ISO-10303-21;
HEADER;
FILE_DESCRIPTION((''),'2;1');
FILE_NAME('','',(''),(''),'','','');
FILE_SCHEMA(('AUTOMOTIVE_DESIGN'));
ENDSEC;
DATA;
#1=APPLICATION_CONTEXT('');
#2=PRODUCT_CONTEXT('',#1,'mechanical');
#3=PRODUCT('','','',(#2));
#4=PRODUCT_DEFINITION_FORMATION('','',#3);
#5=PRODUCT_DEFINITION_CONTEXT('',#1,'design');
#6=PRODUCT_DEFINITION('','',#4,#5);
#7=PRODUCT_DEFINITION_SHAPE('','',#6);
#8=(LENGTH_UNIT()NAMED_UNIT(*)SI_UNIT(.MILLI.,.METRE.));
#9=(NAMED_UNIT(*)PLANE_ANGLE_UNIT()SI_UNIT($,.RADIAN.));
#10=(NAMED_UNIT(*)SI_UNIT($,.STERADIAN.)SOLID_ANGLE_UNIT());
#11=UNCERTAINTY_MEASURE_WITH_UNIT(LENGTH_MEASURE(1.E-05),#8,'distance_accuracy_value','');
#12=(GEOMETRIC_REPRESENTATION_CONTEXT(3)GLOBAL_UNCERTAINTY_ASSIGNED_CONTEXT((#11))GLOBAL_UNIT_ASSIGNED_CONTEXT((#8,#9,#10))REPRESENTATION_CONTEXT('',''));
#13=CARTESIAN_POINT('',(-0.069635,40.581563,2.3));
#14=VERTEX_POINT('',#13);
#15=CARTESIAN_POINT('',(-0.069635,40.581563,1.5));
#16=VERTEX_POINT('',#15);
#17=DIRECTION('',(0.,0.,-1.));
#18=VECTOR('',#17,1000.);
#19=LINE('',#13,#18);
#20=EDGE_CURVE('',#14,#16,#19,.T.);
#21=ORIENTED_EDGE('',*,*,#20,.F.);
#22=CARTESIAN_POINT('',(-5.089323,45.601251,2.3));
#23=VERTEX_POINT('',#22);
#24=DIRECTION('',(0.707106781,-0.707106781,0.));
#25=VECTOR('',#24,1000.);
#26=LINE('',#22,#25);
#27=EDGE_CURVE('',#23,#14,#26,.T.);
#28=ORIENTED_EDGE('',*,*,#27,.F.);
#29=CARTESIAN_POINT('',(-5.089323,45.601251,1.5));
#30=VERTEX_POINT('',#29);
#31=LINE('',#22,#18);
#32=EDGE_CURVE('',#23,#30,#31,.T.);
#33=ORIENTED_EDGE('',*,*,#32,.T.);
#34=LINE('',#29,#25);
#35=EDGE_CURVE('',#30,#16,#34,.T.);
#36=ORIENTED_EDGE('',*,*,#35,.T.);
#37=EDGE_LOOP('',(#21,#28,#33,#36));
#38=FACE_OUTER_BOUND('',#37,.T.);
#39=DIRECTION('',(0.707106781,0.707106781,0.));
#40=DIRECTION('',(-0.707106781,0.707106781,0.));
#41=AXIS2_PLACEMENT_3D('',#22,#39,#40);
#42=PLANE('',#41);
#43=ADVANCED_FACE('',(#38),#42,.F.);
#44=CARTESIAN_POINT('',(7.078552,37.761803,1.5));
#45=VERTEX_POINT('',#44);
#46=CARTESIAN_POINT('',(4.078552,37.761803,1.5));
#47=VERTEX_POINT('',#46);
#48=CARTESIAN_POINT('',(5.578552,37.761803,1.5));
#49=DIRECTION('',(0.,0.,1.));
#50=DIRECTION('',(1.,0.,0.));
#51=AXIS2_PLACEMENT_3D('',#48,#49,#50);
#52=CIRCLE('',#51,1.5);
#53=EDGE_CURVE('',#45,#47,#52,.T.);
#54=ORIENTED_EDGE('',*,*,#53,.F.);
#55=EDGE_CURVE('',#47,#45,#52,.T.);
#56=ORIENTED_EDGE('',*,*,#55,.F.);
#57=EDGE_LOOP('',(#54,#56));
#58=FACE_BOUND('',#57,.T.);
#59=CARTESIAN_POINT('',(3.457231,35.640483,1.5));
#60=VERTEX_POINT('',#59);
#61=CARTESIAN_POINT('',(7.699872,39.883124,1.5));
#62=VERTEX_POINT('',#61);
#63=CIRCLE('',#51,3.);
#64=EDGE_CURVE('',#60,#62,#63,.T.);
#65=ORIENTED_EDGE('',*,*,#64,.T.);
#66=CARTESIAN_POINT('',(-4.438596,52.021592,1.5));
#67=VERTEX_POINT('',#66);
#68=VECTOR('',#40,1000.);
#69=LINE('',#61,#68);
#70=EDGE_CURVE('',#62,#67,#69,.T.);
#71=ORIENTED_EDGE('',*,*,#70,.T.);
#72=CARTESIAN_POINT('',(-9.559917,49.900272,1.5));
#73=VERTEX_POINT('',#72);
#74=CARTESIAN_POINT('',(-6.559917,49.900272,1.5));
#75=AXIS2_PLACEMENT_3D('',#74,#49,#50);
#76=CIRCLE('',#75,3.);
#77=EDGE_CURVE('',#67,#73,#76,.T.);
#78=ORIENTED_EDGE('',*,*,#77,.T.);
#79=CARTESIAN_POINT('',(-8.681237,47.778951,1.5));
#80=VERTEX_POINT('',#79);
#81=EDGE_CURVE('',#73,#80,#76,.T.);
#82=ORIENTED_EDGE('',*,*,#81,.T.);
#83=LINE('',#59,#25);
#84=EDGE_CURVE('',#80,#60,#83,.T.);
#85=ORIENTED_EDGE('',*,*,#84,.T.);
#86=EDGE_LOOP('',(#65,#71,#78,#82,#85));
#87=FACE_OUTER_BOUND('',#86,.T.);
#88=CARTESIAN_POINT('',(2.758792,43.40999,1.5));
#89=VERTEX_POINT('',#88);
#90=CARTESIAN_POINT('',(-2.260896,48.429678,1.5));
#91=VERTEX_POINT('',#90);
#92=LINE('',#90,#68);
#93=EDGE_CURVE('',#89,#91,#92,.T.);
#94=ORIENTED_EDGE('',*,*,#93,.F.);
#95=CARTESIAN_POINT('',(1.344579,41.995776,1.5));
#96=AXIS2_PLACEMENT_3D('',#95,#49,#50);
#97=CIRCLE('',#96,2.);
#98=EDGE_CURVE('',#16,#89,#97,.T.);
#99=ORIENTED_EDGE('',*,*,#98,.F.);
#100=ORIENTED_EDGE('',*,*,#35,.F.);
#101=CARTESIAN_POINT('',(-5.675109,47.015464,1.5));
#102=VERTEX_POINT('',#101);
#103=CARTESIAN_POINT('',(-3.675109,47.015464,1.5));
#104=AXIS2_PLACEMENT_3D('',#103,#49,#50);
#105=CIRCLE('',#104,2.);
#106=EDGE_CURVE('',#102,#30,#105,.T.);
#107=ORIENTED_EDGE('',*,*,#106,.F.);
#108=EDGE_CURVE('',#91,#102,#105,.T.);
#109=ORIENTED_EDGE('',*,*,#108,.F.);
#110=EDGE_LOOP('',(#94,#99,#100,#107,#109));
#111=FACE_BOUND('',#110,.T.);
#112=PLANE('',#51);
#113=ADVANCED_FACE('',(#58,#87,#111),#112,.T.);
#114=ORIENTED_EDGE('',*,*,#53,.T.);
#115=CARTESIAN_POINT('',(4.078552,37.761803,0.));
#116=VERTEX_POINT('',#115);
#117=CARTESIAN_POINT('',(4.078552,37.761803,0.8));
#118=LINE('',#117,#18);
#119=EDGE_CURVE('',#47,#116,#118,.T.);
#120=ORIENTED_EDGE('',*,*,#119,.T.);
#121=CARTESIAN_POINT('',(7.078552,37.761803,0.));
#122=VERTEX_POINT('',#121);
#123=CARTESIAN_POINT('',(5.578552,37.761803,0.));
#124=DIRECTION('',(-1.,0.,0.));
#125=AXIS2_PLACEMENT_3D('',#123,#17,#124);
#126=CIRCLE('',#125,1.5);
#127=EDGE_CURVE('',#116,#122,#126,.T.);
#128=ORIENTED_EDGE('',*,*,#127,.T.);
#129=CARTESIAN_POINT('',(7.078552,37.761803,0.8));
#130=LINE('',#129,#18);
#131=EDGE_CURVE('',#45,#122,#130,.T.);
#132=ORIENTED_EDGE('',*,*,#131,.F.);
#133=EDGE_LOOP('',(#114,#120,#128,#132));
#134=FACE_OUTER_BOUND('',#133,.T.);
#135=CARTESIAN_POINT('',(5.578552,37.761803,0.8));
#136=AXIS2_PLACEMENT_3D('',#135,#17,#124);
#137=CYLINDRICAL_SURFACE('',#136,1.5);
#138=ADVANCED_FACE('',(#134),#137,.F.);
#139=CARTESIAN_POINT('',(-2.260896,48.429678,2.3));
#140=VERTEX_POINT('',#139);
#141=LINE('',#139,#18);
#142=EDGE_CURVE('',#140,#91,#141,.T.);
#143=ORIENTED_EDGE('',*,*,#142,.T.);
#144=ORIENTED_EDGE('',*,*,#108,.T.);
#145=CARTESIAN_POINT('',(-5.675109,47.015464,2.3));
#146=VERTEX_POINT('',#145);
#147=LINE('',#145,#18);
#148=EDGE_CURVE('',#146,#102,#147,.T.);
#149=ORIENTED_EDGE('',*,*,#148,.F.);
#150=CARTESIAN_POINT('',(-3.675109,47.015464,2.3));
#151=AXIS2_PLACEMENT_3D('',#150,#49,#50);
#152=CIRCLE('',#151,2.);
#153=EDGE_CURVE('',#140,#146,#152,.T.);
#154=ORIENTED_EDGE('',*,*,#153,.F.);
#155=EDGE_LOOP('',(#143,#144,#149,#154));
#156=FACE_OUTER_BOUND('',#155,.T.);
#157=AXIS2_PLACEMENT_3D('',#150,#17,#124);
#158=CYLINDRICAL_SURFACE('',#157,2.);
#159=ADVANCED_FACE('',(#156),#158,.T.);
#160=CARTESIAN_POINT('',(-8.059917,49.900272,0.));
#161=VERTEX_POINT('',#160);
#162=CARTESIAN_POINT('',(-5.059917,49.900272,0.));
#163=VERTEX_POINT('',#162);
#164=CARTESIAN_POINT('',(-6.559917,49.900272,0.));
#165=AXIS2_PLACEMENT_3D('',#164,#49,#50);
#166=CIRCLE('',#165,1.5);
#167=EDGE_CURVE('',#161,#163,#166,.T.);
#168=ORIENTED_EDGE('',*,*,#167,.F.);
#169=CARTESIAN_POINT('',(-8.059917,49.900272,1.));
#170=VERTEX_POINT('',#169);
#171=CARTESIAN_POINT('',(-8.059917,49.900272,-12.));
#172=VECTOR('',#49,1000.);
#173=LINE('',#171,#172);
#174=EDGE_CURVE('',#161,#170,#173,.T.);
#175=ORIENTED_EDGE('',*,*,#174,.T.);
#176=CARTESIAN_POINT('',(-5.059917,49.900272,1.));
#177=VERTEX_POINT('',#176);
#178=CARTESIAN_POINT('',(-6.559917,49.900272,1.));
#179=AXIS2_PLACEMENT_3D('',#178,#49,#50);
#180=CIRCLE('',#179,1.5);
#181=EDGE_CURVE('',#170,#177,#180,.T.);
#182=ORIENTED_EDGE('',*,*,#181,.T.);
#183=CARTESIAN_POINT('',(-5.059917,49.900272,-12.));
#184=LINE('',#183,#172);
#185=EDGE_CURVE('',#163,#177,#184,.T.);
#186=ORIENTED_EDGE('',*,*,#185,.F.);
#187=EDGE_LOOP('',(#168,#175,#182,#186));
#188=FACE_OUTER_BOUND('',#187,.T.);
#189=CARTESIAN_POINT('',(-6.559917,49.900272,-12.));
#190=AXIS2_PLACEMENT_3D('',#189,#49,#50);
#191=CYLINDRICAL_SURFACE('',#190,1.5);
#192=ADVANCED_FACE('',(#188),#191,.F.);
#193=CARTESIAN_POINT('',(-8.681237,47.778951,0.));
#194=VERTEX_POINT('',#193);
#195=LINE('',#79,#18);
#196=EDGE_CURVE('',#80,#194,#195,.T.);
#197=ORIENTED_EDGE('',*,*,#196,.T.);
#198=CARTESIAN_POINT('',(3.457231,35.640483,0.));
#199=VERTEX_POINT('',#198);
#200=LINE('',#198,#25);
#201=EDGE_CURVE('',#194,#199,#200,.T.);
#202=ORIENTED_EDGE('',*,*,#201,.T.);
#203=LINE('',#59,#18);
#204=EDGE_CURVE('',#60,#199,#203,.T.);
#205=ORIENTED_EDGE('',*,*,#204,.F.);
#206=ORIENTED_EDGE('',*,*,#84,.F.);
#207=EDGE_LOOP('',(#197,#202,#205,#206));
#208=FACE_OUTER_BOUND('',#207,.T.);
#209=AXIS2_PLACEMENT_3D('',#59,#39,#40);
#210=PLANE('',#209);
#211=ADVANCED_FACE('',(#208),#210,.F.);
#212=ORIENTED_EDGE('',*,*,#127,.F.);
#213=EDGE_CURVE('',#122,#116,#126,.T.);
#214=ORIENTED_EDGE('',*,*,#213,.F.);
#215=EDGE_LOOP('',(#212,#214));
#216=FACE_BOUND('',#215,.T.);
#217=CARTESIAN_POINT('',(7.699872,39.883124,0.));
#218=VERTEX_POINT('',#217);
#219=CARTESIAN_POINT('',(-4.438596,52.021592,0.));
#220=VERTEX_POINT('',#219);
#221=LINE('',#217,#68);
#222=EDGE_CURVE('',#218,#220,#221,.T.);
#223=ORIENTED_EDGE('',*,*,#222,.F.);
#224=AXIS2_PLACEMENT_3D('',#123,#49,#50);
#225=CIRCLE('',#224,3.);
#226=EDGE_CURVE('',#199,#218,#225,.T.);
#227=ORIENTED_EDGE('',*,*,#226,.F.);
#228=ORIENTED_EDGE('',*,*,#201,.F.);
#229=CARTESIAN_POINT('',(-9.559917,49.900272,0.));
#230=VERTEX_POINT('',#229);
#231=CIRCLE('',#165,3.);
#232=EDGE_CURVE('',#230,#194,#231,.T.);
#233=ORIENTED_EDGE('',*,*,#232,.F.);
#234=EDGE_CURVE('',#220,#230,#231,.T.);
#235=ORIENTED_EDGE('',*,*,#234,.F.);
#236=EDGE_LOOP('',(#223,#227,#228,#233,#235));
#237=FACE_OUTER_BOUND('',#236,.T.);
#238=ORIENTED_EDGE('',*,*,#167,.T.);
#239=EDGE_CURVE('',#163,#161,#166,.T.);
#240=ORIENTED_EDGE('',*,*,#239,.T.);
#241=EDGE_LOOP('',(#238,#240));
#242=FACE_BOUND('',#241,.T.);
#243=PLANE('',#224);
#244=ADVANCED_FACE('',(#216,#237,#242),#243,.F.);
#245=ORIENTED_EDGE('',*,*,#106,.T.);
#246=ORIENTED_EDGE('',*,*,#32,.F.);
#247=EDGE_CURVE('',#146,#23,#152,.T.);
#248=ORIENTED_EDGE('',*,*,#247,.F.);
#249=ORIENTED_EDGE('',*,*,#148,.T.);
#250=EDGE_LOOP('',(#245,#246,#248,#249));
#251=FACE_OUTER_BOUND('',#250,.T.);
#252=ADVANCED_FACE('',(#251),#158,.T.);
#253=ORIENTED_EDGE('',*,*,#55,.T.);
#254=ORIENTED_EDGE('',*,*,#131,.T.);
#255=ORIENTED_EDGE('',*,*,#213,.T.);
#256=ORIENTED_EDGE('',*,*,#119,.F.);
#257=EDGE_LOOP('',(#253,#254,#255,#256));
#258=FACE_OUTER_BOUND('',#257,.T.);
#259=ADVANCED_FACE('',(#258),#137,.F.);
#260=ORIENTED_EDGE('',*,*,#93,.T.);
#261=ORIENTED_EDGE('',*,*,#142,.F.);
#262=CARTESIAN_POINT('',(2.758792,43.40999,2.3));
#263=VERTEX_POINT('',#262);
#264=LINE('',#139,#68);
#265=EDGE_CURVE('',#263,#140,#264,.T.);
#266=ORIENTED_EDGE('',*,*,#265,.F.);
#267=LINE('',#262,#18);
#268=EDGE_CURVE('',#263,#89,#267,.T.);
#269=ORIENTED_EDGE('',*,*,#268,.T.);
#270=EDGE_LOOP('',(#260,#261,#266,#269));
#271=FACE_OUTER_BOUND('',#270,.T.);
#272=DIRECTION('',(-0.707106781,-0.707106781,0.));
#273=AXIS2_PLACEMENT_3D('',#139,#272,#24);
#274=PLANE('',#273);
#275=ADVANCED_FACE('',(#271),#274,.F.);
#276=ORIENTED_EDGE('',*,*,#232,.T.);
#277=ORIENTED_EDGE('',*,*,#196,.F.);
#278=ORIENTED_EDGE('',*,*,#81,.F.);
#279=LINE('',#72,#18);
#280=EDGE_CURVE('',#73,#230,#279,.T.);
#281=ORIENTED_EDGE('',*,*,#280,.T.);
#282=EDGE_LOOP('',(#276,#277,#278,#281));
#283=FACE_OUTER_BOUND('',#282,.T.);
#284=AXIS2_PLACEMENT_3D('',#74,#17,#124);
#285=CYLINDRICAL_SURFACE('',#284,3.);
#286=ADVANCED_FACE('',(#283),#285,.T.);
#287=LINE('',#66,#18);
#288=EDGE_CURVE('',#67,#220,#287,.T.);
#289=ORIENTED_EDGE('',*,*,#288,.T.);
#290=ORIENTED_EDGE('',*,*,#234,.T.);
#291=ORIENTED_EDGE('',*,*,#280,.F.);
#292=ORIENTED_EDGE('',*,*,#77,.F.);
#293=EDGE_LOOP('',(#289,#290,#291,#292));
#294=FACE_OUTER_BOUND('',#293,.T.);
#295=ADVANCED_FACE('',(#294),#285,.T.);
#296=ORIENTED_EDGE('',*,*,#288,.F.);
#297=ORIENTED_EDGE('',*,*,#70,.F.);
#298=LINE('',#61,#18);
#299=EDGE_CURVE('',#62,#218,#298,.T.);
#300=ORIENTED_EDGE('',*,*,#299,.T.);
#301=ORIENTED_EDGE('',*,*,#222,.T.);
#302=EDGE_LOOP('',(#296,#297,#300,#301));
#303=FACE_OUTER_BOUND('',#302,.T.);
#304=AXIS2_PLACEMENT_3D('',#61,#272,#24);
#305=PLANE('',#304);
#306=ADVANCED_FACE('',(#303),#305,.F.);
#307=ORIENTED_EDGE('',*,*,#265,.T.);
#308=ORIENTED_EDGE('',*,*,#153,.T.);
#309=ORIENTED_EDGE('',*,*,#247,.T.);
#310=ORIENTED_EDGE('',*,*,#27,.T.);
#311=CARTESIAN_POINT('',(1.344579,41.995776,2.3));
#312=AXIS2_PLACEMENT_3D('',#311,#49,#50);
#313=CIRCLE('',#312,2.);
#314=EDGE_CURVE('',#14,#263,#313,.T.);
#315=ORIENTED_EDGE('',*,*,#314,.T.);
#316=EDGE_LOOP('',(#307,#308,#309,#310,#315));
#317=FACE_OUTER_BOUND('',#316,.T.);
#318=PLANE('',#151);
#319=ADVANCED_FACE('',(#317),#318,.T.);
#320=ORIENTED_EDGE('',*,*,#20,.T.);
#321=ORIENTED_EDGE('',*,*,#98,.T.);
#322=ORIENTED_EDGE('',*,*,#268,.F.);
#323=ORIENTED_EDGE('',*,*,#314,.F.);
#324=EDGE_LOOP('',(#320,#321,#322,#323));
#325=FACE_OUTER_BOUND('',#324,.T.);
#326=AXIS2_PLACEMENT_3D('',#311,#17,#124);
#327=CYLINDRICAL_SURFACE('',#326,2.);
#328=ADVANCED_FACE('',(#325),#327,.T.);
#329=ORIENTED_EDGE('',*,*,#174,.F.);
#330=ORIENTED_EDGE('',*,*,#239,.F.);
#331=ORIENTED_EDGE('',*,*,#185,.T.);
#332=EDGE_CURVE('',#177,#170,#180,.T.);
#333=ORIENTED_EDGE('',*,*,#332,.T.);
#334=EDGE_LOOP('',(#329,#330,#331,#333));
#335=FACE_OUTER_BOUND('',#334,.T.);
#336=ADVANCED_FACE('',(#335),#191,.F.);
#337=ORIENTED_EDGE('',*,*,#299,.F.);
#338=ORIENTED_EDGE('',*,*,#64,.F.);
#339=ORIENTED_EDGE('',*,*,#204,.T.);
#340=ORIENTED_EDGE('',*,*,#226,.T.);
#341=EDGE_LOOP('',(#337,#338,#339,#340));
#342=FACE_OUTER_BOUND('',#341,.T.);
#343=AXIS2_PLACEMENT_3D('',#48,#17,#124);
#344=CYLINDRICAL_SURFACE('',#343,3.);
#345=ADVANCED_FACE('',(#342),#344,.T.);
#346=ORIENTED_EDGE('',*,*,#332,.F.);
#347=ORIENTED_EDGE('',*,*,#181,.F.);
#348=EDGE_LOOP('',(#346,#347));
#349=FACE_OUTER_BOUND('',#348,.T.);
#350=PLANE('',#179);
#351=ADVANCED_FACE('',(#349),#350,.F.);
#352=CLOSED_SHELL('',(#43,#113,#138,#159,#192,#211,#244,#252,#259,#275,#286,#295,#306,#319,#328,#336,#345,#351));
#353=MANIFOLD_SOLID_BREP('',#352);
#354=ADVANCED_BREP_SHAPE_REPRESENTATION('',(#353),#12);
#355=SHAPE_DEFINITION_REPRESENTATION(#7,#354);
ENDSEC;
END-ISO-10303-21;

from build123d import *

# Parameters (mm, degrees)
BOSS_EXTRUDE1_DEPTH = 1.5
BOSS_EXTRUDE3_DEPTH = 0.8
SKETCH4_R           = 1.5
CUT_EXTRUDE1_DEPTH  = 0.8
CUT_EXTRUDE2_START  = -0.5
SKETCH5_R           = 1.5
CUT_EXTRUDE2_DEPTH  = 13
SKETCH6_R           = 1.5
CUT_EXTRUDE3_DEPTH  = 7


with BuildPart() as part:
    # Sketch2 → Boss-Extrude1 (new body)
    with BuildSketch(Plane.XY):
        with BuildLine():
            Line((7.699872028, 39.883123683), (-4.438596359, 52.02159207))
            ThreePointArc((-4.438596359, 52.02159207), (-8.681237046, 52.02159207), (-8.681237046, 47.778951383))
            Line((-8.681237046, 47.778951383), (3.457231341, 35.640482996))
            ThreePointArc((3.457231341, 35.640482996), (7.699872028, 35.640482996), (7.699872028, 39.883123683))
        make_face()
    extrude(amount=BOSS_EXTRUDE1_DEPTH)

    # Sketch3 → Boss-Extrude3 (add)
    with BuildSketch(Plane.XY.offset(1.5)):
        with BuildLine():
            Line((-2.260895514, 48.429677662), (2.758792127, 43.409990022))
            ThreePointArc((2.758792127, 43.409990022), (2.758792127, 40.581562897), (-0.069634998, 40.581562897))
            Line((-0.069634998, 40.581562897), (-5.089322639, 45.601250538))
            ThreePointArc((-5.089322639, 45.601250538), (-5.089322639, 48.429677662), (-2.260895514, 48.429677662))
        make_face()
    extrude(amount=BOSS_EXTRUDE3_DEPTH)

    # Sketch4 → Cut-Extrude1 (cut)
    with BuildSketch(Plane(origin=(0, 0, 0), x_dir=(-1, 0, 0), z_dir=(0, 0, -1))):
        with Locations((-5.578551684, 37.761803339)):
            Circle(SKETCH4_R)
    extrude(amount=-CUT_EXTRUDE1_DEPTH, mode=Mode.SUBTRACT)

    # Sketch5 → Cut-Extrude2 (cut)
    with BuildSketch(Plane.XY.offset(1.5).offset(CUT_EXTRUDE2_START)):
        with Locations((-6.559916703, 49.900271726)):
            Circle(SKETCH5_R)
    extrude(amount=-CUT_EXTRUDE2_DEPTH, mode=Mode.SUBTRACT)

    # Sketch6 → Cut-Extrude3 (cut)
    with BuildSketch(Plane(origin=(0, 0, 0), x_dir=(-1, 0, 0), z_dir=(0, 0, -1))):
        with Locations((-5.578551684, 37.761803339)):
            Circle(SKETCH6_R)
    extrude(amount=-CUT_EXTRUDE3_DEPTH, mode=Mode.SUBTRACT)


solid = part.part
